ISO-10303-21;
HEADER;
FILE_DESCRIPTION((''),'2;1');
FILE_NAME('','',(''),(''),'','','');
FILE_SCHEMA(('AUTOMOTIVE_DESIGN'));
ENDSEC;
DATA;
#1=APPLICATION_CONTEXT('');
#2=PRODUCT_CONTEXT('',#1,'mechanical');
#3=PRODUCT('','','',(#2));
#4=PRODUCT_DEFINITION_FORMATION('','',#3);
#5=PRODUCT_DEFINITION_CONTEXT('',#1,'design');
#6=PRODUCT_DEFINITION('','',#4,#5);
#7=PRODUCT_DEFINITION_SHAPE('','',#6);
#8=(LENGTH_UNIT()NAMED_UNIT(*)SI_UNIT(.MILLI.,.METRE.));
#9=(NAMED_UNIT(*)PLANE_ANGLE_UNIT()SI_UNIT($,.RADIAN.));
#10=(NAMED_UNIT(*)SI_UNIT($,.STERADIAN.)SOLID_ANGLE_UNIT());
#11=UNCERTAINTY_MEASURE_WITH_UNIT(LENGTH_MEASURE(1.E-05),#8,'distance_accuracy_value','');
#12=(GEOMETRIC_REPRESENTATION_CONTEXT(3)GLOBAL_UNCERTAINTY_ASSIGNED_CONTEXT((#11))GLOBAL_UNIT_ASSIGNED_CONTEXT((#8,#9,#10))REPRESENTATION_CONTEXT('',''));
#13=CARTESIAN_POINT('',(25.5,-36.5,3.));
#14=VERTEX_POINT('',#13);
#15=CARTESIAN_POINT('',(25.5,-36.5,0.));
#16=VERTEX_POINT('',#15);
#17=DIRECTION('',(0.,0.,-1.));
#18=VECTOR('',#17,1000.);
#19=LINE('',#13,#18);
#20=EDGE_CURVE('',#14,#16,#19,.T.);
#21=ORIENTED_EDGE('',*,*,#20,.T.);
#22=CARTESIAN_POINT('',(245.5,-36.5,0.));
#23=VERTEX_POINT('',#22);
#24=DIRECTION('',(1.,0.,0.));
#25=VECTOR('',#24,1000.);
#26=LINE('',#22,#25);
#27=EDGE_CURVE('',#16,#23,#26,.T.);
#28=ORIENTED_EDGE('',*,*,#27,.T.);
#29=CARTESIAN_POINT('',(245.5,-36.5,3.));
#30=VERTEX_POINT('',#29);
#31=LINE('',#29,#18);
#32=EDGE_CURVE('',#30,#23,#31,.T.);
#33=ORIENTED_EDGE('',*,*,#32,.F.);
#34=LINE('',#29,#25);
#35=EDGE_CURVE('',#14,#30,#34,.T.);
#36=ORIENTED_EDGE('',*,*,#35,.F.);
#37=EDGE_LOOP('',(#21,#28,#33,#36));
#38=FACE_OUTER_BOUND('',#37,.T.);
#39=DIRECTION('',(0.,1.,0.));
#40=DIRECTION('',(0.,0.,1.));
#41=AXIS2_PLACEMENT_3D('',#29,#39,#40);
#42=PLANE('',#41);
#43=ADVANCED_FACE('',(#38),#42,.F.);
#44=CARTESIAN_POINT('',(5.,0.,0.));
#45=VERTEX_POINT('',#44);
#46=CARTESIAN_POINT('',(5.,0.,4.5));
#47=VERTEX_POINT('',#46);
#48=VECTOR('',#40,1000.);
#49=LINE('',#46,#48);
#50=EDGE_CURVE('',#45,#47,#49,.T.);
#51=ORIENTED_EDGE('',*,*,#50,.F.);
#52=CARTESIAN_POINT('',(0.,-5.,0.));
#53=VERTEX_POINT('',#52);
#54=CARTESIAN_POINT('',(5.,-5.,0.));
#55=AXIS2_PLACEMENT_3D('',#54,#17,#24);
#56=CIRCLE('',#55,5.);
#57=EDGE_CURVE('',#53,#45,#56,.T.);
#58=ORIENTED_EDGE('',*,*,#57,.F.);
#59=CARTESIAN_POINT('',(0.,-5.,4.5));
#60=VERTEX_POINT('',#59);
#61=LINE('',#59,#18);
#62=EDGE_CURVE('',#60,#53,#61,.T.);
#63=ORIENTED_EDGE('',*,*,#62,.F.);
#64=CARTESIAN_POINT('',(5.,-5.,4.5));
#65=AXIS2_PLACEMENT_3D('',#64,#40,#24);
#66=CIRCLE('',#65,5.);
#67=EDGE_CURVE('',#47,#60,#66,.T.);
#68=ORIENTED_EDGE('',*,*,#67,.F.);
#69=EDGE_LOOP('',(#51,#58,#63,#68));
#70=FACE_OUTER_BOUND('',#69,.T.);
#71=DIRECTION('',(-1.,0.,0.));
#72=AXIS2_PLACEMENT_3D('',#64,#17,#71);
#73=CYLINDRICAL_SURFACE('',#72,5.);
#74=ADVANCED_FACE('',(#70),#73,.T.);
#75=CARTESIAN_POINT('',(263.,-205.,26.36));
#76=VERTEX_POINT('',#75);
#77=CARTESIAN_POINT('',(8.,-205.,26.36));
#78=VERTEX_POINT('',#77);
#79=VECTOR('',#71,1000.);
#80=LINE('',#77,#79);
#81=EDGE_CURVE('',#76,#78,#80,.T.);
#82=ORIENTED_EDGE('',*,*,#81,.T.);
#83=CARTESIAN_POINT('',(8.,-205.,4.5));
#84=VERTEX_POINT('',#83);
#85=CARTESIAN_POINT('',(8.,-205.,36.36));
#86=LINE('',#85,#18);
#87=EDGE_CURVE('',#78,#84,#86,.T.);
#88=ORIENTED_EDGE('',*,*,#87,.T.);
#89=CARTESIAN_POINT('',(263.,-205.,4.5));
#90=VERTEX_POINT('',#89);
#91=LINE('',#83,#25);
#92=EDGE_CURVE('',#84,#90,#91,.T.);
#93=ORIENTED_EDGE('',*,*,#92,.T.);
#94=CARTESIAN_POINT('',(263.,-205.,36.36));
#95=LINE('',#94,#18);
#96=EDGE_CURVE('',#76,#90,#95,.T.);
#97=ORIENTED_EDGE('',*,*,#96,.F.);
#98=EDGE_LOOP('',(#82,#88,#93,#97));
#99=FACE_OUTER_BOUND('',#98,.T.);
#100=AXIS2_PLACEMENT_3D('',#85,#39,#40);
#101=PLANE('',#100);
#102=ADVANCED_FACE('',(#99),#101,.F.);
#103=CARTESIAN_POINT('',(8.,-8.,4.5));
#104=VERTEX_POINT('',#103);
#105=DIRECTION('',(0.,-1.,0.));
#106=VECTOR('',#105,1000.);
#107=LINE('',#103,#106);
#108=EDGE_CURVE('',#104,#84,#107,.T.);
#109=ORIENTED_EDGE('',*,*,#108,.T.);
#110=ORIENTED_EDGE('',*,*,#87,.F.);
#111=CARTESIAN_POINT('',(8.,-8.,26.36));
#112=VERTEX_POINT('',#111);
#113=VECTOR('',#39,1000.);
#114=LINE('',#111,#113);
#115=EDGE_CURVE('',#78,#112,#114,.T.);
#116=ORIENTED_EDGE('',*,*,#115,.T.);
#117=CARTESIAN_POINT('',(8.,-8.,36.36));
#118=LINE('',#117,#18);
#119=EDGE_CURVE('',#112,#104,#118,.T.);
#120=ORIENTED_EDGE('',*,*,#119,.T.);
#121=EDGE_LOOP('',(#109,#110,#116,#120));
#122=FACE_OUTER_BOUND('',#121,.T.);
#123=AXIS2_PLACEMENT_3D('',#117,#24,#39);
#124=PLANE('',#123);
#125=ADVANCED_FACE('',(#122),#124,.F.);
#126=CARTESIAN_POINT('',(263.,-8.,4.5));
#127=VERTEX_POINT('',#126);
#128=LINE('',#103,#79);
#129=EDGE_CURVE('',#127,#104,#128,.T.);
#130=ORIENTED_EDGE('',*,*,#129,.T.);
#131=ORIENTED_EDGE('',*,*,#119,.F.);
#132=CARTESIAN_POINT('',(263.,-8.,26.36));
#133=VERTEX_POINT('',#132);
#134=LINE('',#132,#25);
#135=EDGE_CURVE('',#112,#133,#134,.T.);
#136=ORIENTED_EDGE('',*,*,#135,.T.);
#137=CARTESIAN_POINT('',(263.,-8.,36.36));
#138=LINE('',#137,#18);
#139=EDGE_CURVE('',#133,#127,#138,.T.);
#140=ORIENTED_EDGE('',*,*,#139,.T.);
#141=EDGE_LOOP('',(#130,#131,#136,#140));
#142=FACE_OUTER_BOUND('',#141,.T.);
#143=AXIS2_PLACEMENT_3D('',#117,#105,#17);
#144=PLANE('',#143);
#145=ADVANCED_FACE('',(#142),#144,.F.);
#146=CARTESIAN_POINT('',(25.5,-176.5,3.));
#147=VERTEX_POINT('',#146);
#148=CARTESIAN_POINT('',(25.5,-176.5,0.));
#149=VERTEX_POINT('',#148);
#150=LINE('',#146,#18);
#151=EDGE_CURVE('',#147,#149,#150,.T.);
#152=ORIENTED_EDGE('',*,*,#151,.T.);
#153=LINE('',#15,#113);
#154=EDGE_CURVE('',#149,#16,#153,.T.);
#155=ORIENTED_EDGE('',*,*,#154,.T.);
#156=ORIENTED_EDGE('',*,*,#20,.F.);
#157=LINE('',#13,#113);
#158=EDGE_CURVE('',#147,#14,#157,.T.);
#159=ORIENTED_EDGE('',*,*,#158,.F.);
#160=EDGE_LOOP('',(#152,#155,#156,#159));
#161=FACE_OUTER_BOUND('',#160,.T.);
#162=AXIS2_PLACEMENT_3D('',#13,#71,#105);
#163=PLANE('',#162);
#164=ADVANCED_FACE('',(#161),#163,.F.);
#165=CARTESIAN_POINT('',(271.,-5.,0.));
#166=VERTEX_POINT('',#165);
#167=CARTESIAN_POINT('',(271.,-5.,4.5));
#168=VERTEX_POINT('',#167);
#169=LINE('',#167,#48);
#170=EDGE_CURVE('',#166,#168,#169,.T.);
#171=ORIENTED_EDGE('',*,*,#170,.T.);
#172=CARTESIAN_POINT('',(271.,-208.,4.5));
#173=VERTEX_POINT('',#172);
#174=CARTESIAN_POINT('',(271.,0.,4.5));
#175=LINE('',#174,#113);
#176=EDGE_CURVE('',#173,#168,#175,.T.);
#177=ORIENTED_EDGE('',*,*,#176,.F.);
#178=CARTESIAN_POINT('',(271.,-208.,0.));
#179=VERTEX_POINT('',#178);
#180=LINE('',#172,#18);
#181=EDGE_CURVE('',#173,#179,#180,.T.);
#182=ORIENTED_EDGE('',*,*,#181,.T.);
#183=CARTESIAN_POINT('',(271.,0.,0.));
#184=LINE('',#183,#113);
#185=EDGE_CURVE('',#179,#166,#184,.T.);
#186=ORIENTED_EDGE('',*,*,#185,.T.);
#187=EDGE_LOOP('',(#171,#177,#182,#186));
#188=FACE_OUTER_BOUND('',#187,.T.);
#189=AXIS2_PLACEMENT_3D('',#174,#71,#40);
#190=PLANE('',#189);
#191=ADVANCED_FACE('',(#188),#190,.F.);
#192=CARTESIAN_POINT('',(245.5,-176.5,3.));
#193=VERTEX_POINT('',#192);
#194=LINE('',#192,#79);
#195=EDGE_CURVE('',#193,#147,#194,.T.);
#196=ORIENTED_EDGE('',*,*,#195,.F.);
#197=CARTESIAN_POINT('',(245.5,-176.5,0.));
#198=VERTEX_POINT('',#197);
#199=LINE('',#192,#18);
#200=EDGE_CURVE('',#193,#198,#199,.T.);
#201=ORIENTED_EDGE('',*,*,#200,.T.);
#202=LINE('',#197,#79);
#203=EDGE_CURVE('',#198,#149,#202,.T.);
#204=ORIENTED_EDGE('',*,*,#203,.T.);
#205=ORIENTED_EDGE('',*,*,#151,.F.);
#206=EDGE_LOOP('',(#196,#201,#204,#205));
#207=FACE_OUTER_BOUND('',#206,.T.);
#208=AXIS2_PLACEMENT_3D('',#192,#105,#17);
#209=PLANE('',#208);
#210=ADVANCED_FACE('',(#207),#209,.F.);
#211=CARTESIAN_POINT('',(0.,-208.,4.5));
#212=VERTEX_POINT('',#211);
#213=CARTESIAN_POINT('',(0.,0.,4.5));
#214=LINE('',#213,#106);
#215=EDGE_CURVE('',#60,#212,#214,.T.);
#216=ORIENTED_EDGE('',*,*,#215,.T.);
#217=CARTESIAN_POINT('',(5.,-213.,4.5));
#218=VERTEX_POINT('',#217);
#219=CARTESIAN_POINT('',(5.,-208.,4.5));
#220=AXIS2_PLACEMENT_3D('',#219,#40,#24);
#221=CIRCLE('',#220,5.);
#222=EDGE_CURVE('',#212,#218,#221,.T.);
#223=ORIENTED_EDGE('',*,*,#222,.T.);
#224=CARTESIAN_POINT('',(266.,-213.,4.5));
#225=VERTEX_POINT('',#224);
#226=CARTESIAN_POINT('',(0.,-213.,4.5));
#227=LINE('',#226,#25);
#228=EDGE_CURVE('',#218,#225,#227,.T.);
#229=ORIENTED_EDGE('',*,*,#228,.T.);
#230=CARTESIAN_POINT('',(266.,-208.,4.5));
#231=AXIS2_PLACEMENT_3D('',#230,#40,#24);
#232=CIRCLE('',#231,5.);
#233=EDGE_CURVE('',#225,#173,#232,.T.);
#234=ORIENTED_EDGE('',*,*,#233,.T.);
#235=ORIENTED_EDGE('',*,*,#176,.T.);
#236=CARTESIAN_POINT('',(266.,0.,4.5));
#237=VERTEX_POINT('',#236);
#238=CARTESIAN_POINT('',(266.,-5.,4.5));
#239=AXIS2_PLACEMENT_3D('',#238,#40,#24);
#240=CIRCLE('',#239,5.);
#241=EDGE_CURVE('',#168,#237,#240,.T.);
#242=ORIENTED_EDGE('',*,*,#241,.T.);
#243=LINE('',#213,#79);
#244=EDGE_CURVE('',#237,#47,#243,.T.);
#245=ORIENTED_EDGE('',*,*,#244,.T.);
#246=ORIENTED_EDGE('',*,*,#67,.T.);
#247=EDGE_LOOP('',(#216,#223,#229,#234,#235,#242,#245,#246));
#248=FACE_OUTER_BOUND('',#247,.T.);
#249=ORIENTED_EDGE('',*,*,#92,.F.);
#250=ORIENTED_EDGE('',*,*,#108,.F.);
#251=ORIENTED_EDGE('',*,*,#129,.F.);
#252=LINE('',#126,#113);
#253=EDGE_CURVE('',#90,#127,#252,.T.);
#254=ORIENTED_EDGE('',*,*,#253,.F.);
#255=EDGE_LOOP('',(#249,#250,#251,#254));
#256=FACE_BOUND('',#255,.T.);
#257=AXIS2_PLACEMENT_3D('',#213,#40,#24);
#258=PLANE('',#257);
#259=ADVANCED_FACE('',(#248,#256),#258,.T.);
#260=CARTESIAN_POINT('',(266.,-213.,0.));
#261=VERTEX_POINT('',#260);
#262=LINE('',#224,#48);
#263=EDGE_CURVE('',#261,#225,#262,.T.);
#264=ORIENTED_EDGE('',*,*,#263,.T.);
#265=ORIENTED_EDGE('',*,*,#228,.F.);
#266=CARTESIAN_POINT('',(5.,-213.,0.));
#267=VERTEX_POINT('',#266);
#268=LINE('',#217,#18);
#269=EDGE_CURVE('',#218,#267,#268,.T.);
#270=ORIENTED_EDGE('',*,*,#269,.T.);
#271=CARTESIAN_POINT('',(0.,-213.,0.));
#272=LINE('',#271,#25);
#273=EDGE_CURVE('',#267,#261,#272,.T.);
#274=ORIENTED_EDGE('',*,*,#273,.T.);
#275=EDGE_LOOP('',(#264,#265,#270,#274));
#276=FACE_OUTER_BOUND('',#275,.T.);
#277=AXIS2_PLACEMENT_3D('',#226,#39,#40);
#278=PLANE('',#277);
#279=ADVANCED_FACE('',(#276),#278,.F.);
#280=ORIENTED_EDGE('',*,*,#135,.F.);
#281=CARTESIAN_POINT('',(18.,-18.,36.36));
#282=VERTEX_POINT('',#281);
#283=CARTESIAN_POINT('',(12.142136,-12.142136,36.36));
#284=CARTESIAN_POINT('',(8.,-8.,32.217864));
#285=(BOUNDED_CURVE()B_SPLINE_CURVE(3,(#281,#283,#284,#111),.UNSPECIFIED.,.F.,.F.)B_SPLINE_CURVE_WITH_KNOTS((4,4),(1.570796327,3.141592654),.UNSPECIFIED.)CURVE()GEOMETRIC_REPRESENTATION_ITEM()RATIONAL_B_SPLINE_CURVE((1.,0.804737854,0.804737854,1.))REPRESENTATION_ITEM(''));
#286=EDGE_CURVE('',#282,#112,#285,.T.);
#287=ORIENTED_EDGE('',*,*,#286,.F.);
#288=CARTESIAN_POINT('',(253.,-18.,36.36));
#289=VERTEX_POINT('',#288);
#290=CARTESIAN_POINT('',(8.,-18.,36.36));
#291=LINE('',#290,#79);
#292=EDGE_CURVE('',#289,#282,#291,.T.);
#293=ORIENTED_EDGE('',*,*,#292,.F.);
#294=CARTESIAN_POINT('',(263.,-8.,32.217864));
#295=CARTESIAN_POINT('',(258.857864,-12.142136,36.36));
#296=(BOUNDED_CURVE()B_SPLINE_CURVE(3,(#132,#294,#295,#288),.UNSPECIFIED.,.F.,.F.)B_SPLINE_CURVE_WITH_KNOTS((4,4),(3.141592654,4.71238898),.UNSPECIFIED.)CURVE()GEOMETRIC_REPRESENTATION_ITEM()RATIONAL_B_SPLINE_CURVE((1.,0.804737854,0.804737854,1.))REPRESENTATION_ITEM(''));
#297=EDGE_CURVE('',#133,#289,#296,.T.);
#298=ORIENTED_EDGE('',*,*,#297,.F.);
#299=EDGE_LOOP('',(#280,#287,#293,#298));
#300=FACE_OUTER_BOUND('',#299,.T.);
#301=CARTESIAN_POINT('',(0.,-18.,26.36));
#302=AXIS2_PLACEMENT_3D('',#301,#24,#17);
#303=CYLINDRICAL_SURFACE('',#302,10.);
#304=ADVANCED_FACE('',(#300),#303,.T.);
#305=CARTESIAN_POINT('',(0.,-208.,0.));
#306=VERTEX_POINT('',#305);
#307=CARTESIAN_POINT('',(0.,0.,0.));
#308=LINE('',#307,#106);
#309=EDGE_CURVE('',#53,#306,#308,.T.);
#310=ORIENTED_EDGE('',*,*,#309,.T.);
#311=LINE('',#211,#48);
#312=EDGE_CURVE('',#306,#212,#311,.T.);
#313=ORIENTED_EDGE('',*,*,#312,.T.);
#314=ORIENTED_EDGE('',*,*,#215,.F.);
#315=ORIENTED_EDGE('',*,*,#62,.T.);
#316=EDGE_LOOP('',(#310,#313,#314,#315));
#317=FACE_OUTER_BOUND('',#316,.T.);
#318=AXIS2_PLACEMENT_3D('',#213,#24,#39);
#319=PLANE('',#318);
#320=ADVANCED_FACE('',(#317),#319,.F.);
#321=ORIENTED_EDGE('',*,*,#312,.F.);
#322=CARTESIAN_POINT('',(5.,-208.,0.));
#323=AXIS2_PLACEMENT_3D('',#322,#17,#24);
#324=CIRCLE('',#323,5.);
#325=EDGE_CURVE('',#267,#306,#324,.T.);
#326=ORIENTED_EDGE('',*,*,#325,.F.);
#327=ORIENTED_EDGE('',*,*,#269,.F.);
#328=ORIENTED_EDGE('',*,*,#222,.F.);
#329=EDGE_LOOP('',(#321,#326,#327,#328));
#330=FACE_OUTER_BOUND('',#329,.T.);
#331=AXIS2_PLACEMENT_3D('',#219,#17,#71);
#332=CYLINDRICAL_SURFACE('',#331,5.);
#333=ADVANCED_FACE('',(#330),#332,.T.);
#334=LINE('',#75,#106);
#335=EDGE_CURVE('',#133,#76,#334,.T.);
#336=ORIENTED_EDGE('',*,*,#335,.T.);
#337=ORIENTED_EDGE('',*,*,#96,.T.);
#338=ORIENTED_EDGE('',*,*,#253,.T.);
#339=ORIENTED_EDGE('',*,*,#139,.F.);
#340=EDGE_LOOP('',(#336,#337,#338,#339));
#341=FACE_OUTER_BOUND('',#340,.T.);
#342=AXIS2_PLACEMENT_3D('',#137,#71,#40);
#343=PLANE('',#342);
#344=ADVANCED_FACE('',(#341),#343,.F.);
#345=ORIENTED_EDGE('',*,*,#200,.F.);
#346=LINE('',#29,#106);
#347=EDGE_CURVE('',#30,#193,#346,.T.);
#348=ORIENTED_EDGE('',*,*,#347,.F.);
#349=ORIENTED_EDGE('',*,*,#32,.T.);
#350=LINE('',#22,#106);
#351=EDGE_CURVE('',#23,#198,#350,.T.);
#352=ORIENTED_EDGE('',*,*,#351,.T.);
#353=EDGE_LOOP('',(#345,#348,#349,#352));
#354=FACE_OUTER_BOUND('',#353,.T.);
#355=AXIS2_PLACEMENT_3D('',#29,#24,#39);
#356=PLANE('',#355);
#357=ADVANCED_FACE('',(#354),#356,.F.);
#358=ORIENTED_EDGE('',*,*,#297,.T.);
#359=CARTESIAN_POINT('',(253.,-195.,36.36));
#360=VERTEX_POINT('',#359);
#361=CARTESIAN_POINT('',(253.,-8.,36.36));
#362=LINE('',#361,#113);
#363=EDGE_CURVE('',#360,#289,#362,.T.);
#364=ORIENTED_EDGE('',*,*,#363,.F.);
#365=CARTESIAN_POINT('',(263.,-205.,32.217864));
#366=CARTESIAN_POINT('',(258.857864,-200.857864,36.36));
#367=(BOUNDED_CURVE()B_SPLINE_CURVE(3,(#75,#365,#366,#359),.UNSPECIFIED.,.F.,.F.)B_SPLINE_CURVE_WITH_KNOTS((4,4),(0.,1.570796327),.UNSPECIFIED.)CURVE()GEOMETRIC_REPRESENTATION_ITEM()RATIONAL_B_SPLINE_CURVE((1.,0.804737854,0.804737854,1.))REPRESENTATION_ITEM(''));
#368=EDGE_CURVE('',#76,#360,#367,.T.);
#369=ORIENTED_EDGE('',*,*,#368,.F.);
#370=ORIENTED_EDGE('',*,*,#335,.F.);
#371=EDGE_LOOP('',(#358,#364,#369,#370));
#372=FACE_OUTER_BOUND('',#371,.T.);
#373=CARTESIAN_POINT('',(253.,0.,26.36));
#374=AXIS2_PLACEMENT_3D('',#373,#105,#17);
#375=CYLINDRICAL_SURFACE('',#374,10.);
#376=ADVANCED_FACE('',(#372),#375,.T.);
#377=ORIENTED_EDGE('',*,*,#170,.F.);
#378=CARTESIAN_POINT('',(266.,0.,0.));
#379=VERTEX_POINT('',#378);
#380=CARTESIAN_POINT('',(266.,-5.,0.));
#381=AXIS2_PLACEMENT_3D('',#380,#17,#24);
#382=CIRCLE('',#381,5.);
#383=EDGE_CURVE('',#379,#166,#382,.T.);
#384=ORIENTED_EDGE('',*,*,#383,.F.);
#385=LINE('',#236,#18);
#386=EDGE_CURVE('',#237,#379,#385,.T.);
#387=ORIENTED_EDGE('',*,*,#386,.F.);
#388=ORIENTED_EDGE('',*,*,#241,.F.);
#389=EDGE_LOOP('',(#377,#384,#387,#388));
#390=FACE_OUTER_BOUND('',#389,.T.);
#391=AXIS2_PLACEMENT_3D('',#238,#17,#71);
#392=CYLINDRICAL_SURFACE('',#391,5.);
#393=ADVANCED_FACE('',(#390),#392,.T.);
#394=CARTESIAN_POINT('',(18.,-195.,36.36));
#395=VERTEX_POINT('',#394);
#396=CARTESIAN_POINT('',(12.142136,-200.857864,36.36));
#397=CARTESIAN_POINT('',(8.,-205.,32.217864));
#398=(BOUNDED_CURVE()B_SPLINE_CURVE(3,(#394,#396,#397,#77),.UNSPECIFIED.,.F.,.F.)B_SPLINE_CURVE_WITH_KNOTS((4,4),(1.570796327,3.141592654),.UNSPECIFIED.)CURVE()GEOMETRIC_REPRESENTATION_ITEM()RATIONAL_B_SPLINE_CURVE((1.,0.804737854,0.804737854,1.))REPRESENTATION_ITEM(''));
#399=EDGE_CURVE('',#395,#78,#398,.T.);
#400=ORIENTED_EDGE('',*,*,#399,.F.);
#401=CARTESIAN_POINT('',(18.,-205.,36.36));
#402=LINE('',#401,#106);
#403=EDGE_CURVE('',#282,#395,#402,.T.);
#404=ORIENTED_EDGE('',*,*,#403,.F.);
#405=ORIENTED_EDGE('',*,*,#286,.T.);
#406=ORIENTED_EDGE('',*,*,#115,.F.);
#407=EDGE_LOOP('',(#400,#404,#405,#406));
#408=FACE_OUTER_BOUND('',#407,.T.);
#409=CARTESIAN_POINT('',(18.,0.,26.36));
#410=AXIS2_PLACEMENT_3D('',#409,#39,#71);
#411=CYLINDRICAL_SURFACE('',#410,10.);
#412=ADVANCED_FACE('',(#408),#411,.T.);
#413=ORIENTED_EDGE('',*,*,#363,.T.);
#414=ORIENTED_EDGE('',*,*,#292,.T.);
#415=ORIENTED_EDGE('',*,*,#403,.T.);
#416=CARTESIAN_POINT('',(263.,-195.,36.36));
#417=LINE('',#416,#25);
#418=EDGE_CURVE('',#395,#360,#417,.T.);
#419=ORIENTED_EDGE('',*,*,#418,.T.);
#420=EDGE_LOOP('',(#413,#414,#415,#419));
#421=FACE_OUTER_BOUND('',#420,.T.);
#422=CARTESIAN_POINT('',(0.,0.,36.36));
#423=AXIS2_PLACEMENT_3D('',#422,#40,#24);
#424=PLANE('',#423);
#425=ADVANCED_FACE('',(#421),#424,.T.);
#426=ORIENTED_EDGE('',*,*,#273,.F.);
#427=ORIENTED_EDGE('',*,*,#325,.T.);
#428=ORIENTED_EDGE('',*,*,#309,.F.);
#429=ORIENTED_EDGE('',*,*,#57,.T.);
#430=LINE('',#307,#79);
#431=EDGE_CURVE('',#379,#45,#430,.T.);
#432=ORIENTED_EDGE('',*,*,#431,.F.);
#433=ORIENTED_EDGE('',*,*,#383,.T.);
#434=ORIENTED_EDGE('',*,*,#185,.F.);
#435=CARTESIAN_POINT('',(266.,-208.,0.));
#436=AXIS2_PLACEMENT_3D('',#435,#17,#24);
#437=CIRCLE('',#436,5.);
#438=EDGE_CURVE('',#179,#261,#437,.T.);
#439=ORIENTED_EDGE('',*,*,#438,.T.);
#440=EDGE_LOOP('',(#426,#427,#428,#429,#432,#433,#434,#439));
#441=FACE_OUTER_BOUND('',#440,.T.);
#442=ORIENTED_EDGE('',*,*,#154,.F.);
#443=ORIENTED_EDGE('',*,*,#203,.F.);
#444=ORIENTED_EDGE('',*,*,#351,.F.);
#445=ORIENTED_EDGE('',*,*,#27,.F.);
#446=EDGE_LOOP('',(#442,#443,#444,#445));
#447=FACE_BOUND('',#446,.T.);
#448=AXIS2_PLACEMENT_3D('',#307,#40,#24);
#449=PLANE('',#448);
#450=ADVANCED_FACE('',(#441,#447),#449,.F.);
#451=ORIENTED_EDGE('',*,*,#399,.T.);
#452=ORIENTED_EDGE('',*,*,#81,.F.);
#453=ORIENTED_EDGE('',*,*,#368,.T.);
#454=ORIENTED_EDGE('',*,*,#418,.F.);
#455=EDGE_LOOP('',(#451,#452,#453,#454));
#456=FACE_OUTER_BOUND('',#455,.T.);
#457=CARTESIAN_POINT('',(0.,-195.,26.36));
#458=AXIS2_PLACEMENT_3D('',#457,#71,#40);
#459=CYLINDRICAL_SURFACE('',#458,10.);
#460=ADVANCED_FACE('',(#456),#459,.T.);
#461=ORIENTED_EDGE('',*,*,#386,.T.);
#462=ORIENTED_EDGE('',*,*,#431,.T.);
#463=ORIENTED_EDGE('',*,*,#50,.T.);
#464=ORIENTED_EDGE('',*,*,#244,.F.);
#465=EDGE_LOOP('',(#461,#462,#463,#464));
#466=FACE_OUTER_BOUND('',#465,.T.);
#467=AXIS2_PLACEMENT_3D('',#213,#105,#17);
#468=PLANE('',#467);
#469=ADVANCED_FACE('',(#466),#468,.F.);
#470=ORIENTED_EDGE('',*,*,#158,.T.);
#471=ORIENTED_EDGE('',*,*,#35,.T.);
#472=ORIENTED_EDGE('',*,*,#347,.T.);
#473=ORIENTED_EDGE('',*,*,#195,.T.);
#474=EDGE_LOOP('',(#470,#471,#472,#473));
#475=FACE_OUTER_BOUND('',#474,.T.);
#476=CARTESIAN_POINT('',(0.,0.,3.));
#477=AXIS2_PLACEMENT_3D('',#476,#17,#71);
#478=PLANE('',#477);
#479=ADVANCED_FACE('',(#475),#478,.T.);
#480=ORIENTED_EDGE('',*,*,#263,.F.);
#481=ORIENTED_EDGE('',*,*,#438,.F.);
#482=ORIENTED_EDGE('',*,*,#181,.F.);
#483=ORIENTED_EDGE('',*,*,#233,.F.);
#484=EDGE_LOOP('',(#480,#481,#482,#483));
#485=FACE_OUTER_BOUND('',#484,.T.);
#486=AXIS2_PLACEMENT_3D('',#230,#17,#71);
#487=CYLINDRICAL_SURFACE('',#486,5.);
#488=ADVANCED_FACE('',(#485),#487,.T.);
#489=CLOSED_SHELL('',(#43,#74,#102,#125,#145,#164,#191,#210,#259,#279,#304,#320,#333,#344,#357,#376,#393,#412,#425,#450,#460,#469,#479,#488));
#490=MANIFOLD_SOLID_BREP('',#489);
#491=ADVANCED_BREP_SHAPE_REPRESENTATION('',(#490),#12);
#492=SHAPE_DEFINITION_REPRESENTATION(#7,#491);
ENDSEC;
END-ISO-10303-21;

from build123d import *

# Parameters (mm, degrees)
SKETCH_1_W          = 271
SKETCH_1_H          = 213
EXTRUDE_1_DEPTH     = 4.5
SKETCH_2_W          = 255
SKETCH_2_H          = 197
EXTRUDE_2_DEPTH     = 31.86
FILLET_1_R          = 10
FILLET_2_R          = 5
SKETCH_4_W          = 220
SKETCH_4_H          = 140
CUT_EXTRUDE_1_DEPTH = 3


with BuildPart() as part:
    # 草图1 → 凸台-拉伸1 (new body)
    with BuildSketch(Plane.XY):
        with Locations((135.5, -106.5)):
            Rectangle(SKETCH_1_W, SKETCH_1_H)
    extrude(amount=EXTRUDE_1_DEPTH)

    # 草图2 → 凸台-拉伸2 (add)
    with BuildSketch(Plane.XY.offset(4.5)):
        with Locations((135.5, -106.5)):
            Rectangle(SKETCH_2_W, SKETCH_2_H)
    extrude(amount=EXTRUDE_2_DEPTH)

    # 圆角1
    fillet_1_edges = [part.edges().sort_by_distance(p)[0] for p in [
        (263, -106.5, 36.36),
        (135.5, -8, 36.36),
        (8, -106.5, 36.36),
        (135.5, -205, 36.36),
    ]]
    fillet(fillet_1_edges, radius=FILLET_1_R)

    # 圆角2
    fillet_2_edges = [part.edges().sort_by_distance(p)[0] for p in [
        (0, 0, 2.25),
        (271, 0, 2.25),
        (271, -213, 2.25),
        (0, -213, 2.25),
    ]]
    fillet(fillet_2_edges, radius=FILLET_2_R)

    # 草图4 → 切除-拉伸1 (cut)
    with BuildSketch(Plane(origin=(0, 0, 0), x_dir=(-1, 0, 0), z_dir=(0, 0, -1))):
        with Locations((-135.5, -106.5)):
            Rectangle(SKETCH_4_W, SKETCH_4_H)
    extrude(amount=-CUT_EXTRUDE_1_DEPTH, mode=Mode.SUBTRACT)


solid = part.part
